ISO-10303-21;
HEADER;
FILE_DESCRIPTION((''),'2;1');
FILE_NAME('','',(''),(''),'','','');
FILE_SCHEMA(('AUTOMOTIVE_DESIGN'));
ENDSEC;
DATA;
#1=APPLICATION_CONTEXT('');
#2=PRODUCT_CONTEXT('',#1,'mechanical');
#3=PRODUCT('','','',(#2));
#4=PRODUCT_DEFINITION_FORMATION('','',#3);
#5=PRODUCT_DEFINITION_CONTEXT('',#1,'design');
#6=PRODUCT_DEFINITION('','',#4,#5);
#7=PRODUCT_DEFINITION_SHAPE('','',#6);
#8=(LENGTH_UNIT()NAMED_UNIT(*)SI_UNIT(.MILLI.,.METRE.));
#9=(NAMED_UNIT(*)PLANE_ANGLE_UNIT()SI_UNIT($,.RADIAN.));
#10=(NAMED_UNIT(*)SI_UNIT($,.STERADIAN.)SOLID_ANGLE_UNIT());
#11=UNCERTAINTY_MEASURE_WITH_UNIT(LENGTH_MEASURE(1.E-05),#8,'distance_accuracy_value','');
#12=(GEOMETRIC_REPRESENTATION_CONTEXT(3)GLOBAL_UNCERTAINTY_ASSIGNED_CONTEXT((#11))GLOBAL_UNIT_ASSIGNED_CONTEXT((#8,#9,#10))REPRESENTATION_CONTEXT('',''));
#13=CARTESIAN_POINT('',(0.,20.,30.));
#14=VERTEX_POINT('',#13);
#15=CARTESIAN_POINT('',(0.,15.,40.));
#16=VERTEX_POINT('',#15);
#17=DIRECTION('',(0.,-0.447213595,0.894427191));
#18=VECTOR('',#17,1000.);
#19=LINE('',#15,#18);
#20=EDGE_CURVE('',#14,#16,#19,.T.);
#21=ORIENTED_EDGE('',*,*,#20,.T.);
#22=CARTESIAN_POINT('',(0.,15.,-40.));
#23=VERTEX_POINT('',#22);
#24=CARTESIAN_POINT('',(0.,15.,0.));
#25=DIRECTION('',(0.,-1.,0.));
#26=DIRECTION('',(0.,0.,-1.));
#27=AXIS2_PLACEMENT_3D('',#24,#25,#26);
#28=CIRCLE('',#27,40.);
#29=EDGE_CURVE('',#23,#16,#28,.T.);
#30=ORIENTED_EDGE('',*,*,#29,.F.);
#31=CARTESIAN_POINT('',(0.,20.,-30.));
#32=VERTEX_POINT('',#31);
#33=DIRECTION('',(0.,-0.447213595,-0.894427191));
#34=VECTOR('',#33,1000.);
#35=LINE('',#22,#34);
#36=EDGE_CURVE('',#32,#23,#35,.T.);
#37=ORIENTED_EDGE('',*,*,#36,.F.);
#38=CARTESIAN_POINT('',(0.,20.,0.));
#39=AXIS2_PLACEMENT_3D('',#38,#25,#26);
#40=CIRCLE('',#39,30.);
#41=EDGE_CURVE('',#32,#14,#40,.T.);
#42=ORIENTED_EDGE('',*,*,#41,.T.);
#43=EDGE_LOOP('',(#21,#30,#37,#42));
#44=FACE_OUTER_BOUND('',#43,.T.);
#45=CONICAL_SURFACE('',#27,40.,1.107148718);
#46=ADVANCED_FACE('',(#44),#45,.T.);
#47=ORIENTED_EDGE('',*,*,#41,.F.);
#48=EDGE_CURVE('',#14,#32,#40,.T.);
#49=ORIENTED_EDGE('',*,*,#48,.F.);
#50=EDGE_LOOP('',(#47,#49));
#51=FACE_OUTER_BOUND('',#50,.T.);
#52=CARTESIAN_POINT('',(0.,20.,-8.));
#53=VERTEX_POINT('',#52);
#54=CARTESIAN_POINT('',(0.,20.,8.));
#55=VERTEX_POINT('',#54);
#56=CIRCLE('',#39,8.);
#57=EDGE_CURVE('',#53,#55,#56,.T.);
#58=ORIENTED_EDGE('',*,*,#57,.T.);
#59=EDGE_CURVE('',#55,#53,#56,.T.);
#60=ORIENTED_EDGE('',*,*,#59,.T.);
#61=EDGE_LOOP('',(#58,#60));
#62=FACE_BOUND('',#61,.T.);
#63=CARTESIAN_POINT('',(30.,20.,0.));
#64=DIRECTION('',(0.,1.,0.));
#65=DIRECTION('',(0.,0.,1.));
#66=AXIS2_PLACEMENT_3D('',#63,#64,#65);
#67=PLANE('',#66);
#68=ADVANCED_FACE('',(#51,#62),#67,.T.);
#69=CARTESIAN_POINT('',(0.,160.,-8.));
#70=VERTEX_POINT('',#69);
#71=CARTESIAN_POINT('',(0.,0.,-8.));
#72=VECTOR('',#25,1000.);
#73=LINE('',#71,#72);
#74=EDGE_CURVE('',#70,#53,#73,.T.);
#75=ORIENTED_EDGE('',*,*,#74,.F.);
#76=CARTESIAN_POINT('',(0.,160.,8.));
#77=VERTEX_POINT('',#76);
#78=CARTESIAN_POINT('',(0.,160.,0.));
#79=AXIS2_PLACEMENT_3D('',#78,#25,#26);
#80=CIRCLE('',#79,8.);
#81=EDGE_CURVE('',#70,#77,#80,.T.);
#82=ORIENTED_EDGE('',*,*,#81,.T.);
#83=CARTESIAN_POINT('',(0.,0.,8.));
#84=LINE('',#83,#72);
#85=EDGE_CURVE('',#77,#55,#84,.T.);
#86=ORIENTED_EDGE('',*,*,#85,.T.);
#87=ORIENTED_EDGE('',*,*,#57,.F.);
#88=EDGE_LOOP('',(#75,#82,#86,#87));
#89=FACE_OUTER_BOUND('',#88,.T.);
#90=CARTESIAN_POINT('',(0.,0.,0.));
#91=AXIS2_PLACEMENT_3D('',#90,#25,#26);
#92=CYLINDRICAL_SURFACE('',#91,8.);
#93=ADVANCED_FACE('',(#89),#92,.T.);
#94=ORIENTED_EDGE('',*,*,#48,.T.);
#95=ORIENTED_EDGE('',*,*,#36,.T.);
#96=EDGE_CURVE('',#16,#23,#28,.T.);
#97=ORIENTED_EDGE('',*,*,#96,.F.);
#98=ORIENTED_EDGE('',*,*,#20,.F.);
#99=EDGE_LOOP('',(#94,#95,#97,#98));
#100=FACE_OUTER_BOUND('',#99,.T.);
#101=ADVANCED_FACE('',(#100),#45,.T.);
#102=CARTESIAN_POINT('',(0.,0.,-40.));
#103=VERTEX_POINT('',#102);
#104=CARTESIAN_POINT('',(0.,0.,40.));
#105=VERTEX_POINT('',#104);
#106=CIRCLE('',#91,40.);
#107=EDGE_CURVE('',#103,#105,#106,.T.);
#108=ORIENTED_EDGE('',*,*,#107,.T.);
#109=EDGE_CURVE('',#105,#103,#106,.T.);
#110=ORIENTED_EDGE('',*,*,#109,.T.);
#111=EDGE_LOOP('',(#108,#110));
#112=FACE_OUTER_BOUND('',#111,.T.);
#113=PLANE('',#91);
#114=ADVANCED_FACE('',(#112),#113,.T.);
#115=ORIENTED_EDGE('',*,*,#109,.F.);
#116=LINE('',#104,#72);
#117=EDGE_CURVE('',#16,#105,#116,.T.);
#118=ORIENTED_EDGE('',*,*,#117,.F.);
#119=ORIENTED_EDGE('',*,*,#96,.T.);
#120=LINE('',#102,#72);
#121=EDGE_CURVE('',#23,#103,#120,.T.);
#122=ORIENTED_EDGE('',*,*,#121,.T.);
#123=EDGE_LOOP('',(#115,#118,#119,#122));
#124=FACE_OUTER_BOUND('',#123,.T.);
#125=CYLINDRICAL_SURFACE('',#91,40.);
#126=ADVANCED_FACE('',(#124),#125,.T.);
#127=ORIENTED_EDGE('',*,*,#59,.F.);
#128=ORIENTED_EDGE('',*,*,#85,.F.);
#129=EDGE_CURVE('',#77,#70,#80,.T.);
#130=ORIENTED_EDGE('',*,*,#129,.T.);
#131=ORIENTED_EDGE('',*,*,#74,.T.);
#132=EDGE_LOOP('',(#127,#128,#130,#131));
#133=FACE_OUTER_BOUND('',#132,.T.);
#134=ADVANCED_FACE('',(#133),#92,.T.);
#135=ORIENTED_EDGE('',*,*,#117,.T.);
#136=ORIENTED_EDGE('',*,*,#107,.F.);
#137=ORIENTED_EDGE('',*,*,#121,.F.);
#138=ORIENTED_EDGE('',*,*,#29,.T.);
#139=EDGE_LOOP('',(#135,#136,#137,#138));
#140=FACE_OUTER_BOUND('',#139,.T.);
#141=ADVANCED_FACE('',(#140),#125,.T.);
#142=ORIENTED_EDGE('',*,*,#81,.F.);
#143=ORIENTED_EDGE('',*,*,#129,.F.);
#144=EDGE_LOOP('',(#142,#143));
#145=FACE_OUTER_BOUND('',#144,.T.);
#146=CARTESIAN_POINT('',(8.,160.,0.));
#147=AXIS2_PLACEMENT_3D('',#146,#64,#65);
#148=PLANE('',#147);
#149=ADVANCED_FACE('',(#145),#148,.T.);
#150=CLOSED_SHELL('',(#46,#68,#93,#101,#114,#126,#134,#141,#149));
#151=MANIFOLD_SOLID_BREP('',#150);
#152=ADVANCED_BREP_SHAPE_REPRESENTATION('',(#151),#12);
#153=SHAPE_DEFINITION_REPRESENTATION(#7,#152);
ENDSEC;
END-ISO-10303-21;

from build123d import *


with BuildPart() as part:
    # 草图1 → 旋转1 (revolve)
    with BuildSketch(Plane.XY, mode=Mode.PRIVATE) as revolve_1_sk:
        Polygon((0, 0), (40, 0), (40, 15), (30, 20), (8, 20), (8, 160), (0, 160), align=None)
    revolve(revolve_1_sk.sketch.rotate(Axis((0, 0, 0), (0, 1, 0)), 90), axis=Axis((0, 0, 0), (0, 1, 0)))


solid = part.part
